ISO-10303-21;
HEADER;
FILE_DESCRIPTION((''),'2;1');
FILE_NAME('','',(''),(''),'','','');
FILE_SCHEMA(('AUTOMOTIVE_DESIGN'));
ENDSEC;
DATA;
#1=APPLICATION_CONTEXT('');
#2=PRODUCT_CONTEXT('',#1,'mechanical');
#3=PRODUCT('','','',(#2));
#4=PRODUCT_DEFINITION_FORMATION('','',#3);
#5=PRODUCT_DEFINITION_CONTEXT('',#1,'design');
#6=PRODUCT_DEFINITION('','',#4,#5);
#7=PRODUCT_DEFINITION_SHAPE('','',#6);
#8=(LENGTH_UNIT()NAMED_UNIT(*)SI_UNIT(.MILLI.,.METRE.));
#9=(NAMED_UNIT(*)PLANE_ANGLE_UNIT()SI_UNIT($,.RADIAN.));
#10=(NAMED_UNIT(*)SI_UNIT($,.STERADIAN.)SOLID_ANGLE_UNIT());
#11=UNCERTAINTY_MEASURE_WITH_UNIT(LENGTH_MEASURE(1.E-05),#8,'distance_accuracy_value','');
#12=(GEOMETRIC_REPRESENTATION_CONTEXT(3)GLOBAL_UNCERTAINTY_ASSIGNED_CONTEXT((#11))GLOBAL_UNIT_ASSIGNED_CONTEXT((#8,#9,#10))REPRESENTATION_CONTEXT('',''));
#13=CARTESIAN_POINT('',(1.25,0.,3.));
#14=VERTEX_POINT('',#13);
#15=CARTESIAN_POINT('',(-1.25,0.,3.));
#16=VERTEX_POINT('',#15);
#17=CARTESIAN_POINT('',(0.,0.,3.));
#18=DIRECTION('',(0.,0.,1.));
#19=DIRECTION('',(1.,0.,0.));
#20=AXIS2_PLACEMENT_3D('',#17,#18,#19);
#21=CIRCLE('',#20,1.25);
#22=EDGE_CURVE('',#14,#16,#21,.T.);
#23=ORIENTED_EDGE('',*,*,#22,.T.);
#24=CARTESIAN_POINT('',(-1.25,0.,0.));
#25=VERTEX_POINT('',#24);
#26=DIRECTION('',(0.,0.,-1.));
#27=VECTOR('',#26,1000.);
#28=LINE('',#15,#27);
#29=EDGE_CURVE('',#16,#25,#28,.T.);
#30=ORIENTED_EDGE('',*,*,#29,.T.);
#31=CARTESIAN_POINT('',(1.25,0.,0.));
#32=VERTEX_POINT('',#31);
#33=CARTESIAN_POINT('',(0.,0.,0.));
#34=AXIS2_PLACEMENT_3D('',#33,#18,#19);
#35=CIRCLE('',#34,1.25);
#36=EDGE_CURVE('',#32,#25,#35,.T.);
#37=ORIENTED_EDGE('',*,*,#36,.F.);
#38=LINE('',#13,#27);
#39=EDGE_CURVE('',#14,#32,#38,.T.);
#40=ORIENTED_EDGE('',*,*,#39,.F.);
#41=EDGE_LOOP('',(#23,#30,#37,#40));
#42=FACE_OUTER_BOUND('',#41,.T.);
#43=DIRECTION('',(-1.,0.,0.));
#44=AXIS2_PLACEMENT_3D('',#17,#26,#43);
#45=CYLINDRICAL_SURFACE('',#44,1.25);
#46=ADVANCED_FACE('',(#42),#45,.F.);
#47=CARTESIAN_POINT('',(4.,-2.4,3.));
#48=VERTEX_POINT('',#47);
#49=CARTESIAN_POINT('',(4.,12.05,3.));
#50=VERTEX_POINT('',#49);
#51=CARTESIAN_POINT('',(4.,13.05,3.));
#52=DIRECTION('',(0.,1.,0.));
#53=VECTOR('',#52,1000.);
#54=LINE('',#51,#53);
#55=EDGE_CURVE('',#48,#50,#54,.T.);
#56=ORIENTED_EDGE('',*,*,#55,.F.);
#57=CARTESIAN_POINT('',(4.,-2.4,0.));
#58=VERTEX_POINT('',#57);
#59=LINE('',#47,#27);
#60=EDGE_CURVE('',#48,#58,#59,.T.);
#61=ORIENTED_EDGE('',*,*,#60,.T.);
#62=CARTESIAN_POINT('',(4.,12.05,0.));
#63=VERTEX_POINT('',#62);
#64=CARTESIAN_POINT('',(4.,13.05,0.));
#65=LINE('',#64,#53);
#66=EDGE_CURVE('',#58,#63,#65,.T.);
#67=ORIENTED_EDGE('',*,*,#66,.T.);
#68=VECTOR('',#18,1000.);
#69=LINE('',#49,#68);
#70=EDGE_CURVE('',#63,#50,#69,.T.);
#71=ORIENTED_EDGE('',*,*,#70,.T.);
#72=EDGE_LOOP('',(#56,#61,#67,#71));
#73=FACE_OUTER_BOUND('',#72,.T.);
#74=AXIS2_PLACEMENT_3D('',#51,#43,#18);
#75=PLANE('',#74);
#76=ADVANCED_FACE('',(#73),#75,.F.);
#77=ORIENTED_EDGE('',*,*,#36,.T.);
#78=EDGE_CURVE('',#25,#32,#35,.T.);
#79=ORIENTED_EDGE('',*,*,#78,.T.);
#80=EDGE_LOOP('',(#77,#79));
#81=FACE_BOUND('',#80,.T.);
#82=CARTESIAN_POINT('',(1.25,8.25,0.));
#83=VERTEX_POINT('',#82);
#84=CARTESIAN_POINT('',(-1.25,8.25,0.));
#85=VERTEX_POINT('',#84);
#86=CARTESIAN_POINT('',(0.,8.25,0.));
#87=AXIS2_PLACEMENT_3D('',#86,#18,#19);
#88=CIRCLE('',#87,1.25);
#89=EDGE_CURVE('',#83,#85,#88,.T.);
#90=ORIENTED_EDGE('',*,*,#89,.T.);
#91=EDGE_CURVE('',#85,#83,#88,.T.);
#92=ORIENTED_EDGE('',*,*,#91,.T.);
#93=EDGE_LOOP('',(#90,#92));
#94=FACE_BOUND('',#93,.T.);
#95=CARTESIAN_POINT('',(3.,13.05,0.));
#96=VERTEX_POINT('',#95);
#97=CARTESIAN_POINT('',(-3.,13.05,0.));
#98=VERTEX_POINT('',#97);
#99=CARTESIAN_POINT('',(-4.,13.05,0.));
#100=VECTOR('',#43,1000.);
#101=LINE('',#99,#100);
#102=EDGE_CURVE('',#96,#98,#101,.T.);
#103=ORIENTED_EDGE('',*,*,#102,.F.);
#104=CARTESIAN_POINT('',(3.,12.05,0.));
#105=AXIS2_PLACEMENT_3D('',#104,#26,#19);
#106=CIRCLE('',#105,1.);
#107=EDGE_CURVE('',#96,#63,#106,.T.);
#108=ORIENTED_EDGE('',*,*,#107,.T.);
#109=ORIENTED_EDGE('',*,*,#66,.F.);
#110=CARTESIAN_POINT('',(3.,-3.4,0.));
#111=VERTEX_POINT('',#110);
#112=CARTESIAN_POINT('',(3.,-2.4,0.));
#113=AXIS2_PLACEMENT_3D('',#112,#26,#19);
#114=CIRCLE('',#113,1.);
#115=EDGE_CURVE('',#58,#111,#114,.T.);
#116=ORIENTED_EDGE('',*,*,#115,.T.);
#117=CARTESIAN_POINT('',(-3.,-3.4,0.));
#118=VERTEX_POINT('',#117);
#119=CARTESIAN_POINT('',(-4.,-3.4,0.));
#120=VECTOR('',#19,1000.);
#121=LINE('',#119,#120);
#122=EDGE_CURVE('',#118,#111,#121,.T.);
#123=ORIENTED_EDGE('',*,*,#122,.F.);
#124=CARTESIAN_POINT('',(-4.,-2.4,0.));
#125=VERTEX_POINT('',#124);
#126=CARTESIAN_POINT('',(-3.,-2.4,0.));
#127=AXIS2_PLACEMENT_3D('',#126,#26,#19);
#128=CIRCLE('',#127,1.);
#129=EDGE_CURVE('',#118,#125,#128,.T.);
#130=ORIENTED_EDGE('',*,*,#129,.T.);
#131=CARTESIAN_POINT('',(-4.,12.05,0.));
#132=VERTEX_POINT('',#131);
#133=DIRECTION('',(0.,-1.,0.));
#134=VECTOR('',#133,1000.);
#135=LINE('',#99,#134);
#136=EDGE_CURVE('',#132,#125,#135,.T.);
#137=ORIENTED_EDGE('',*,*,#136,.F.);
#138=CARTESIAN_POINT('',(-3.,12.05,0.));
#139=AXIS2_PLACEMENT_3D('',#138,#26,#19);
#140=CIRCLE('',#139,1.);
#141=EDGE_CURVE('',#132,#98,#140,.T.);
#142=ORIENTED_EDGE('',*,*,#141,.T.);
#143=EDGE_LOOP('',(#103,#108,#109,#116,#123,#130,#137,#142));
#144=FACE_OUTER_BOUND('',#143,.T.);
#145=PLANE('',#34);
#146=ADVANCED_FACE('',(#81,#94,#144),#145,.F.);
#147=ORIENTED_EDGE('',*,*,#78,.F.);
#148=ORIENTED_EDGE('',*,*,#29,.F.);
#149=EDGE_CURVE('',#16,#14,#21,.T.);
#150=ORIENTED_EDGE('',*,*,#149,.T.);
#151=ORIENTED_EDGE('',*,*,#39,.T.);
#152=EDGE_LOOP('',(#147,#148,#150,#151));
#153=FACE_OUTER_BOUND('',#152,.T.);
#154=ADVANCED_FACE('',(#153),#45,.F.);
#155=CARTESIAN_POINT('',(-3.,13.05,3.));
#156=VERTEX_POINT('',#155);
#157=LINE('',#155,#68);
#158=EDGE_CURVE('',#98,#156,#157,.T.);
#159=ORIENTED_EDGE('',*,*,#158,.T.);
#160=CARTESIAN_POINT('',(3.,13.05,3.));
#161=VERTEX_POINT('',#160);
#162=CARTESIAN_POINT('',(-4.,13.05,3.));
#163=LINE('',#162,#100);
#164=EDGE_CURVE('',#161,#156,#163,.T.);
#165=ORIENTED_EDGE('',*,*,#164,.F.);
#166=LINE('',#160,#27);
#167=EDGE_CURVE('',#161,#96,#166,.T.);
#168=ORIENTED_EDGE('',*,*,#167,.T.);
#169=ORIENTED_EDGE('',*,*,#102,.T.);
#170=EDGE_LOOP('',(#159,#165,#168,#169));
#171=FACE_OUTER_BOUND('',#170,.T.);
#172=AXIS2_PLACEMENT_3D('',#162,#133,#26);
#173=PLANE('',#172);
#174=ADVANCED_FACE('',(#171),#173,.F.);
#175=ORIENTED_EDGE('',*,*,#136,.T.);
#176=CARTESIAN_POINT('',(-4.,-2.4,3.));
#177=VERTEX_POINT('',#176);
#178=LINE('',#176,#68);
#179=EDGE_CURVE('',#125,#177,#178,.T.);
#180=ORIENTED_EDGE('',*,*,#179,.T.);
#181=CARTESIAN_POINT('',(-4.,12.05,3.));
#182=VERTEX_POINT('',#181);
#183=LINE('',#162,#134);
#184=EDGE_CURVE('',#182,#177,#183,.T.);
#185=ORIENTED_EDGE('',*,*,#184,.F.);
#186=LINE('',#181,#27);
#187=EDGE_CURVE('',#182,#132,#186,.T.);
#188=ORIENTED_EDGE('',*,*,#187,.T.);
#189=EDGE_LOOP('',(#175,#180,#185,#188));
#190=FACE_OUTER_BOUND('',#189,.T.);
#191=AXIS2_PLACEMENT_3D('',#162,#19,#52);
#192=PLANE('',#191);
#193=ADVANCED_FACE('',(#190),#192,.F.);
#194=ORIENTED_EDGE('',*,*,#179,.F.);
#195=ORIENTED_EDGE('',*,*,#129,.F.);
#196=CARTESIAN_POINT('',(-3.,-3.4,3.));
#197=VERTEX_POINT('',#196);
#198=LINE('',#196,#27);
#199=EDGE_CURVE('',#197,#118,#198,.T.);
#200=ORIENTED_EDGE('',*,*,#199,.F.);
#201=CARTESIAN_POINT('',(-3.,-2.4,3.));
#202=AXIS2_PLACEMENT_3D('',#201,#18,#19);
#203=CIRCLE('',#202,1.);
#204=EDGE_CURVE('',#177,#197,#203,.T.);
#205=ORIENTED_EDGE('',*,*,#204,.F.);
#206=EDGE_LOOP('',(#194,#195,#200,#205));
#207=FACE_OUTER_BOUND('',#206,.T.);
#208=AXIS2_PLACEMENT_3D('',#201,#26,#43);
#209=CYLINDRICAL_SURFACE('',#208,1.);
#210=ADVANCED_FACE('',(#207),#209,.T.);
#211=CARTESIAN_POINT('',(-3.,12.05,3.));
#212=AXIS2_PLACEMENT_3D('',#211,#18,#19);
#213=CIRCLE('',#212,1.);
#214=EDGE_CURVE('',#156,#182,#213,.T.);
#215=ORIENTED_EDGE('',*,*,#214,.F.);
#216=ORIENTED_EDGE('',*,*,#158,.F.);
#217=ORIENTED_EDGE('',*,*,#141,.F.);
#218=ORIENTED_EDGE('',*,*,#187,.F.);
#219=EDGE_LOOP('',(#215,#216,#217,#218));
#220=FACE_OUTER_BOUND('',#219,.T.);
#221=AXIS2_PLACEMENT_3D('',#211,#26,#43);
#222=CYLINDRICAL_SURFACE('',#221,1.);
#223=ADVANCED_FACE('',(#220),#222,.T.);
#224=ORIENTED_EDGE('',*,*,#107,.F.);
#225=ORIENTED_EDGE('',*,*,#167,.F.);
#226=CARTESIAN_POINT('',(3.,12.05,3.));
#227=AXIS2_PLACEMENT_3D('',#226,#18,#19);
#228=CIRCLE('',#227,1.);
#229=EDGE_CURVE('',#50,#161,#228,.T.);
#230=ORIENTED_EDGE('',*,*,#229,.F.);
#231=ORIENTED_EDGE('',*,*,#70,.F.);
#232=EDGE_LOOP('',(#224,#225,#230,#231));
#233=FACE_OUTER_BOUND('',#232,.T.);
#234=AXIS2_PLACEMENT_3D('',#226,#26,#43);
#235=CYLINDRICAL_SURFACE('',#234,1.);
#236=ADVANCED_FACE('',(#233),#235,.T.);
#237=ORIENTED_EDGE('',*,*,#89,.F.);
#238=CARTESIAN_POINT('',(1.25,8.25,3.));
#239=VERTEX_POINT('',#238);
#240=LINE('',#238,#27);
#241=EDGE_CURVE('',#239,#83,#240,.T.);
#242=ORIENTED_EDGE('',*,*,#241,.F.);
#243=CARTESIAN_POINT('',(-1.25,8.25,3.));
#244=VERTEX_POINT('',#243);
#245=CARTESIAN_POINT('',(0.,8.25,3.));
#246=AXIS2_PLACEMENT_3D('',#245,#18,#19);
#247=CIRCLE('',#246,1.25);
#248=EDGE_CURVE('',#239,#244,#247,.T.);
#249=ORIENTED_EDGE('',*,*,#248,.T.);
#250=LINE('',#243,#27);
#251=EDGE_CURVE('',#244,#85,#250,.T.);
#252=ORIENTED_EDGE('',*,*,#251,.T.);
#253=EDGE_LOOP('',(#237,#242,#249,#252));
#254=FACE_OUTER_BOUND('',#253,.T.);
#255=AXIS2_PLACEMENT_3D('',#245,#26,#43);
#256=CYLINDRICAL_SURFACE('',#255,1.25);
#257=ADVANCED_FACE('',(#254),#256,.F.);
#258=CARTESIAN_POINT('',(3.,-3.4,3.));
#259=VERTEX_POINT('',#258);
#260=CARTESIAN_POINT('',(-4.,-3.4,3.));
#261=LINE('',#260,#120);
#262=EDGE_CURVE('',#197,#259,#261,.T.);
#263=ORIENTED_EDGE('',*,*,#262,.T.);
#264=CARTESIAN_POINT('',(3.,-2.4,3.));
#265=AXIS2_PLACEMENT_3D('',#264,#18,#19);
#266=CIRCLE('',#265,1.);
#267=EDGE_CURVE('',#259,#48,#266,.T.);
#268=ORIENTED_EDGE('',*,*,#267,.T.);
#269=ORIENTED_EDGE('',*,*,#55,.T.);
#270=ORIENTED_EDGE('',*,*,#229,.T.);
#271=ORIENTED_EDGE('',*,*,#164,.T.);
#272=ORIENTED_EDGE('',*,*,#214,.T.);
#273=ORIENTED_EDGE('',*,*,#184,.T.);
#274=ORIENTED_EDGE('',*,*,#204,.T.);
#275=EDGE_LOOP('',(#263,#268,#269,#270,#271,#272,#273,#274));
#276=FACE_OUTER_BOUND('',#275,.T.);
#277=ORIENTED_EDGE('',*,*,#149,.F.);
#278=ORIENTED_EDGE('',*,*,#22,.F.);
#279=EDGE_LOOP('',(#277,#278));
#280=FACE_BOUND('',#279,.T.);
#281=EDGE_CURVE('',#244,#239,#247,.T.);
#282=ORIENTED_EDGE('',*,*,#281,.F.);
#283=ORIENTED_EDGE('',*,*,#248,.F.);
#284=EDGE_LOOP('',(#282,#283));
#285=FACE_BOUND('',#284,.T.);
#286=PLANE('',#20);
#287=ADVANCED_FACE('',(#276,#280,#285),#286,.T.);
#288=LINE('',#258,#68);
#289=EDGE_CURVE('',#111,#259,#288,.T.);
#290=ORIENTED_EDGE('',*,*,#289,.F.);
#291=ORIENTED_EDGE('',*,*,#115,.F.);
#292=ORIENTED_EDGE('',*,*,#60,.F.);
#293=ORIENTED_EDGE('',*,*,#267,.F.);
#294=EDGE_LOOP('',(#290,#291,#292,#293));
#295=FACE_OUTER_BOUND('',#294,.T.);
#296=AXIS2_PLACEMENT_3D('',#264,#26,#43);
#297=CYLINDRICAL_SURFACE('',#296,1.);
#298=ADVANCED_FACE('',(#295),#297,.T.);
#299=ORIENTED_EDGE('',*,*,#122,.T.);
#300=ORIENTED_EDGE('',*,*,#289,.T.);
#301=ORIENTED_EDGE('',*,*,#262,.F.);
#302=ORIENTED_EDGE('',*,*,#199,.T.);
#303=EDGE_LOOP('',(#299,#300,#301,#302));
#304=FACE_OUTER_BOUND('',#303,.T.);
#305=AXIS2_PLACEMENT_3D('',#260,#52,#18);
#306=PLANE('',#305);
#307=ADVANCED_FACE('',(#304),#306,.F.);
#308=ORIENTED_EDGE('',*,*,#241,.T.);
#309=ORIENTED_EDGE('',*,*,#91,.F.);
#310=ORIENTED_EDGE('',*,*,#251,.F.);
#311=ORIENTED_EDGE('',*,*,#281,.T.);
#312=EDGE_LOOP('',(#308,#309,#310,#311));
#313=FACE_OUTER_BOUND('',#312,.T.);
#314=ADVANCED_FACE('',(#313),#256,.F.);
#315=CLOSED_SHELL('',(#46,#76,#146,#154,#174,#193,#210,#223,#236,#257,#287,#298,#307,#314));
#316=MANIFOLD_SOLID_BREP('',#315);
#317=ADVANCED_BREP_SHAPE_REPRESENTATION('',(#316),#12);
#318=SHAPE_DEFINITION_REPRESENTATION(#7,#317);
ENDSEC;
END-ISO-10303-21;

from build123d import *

# Parameters (mm, degrees)
SKETCH_1_W      = 8
SKETCH_1_H      = 16.45
SKETCH_1_R      = 1.25
EXTRUDE_1_DEPTH = 3
FILLET_1_R      = 1


with BuildPart() as part:
    # 草图1 → 凸台-拉伸1 (new body)
    with BuildSketch(Plane.XY):
        with Locations((0, 4.825)):
            Rectangle(SKETCH_1_W, SKETCH_1_H)
        Circle(SKETCH_1_R, mode=Mode.SUBTRACT)
        with Locations((0, 8.25)):
            Circle(SKETCH_1_R, mode=Mode.SUBTRACT)
    extrude(amount=EXTRUDE_1_DEPTH)

    # 圆角1
    fillet_1_edges = [part.edges().sort_by_distance(p)[0] for p in [
        (4, -3.4, 1.5),
        (-4, -3.4, 1.5),
        (-4, 13.05, 1.5),
        (4, 13.05, 1.5),
    ]]
    fillet(fillet_1_edges, radius=FILLET_1_R)


solid = part.part
